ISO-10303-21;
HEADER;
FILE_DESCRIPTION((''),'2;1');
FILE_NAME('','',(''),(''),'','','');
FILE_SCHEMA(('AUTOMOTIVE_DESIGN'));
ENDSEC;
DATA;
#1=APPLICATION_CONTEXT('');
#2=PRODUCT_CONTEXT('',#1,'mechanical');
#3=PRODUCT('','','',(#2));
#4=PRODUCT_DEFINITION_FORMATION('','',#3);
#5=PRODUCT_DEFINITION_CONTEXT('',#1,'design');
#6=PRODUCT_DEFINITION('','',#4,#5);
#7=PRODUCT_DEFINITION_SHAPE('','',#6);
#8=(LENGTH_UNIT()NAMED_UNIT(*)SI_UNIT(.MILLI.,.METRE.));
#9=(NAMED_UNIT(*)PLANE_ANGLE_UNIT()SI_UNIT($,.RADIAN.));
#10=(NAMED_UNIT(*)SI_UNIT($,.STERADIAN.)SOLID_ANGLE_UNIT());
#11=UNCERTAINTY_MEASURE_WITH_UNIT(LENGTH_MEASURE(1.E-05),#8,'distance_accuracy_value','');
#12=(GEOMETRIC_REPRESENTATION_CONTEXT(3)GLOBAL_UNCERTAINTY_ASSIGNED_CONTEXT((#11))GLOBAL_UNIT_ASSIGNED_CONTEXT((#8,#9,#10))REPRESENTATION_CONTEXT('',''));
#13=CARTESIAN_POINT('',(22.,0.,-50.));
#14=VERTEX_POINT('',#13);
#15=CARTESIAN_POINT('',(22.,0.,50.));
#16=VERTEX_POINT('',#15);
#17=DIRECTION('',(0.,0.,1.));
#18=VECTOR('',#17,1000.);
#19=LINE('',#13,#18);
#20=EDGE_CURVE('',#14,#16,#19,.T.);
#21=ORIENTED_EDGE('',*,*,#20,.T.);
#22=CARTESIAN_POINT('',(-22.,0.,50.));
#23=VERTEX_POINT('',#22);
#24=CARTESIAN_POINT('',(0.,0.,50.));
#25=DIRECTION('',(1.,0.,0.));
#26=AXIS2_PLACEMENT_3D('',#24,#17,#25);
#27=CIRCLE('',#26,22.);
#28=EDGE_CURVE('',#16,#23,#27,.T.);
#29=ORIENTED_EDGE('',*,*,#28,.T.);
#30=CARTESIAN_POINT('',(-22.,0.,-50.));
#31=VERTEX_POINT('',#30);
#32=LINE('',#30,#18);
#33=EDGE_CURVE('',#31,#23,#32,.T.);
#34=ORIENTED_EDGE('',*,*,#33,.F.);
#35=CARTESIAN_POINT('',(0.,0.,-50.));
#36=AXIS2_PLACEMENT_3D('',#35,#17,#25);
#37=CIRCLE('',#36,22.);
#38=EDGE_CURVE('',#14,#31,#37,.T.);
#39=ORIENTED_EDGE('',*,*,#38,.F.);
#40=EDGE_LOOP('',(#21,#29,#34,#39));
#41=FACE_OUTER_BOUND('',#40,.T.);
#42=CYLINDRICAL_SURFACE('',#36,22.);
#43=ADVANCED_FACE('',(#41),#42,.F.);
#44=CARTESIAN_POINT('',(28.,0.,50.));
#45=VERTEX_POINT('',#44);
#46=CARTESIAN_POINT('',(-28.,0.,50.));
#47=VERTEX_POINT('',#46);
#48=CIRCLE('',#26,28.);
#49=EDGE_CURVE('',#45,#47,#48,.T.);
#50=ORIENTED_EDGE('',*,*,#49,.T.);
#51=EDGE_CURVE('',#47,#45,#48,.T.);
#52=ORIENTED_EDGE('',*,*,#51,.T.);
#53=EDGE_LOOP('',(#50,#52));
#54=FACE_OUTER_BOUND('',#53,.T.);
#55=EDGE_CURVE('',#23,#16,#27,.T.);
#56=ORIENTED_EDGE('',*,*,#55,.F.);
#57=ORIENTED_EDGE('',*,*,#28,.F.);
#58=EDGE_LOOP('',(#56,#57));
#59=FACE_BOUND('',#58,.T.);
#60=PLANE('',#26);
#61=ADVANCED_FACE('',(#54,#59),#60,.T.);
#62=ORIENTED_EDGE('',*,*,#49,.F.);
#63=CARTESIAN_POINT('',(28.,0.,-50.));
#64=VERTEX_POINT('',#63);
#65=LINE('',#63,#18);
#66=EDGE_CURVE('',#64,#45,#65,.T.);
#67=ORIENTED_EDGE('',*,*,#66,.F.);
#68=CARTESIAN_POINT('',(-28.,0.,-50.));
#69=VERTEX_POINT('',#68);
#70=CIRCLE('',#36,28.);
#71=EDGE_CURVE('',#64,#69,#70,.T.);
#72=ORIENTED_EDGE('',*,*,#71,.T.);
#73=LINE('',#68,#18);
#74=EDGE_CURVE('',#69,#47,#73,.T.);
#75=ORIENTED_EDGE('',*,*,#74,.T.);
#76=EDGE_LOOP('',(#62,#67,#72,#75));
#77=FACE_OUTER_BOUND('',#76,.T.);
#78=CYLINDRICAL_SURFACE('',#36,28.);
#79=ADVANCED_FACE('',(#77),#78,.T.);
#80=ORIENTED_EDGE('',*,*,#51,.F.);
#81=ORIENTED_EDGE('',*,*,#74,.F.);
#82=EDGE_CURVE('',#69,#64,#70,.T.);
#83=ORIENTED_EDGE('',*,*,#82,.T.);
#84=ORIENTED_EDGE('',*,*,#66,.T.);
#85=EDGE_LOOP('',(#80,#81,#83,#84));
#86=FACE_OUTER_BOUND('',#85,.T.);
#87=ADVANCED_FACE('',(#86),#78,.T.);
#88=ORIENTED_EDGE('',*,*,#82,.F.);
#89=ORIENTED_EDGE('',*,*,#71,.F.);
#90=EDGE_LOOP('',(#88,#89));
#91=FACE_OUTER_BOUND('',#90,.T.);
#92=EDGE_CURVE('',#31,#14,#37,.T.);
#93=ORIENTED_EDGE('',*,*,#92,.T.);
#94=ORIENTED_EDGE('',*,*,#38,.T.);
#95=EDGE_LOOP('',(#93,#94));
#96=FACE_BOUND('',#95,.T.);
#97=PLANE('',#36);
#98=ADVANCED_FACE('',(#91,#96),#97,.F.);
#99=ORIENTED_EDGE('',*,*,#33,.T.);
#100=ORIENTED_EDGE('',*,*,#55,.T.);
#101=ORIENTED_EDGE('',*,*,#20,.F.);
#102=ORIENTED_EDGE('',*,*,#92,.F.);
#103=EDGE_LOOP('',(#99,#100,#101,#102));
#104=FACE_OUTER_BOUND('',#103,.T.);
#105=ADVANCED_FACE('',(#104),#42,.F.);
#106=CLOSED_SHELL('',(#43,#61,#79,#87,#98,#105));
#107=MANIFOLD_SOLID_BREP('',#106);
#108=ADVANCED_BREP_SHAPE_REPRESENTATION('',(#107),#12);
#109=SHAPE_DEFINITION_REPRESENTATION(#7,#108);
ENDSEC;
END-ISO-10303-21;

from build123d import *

# Parameters (mm, degrees)
SKETCH_1_R      = 28
SKETCH_1_R_2    = 22
EXTRUDE_1_DEPTH = 50


with BuildPart() as part:
    # 草图1 → 凸台-拉伸1 (new, symmetric)
    with BuildSketch(Plane.XY):
        Circle(SKETCH_1_R)
        Circle(SKETCH_1_R_2, mode=Mode.SUBTRACT)
    extrude(amount=EXTRUDE_1_DEPTH, both=True)


solid = part.part
